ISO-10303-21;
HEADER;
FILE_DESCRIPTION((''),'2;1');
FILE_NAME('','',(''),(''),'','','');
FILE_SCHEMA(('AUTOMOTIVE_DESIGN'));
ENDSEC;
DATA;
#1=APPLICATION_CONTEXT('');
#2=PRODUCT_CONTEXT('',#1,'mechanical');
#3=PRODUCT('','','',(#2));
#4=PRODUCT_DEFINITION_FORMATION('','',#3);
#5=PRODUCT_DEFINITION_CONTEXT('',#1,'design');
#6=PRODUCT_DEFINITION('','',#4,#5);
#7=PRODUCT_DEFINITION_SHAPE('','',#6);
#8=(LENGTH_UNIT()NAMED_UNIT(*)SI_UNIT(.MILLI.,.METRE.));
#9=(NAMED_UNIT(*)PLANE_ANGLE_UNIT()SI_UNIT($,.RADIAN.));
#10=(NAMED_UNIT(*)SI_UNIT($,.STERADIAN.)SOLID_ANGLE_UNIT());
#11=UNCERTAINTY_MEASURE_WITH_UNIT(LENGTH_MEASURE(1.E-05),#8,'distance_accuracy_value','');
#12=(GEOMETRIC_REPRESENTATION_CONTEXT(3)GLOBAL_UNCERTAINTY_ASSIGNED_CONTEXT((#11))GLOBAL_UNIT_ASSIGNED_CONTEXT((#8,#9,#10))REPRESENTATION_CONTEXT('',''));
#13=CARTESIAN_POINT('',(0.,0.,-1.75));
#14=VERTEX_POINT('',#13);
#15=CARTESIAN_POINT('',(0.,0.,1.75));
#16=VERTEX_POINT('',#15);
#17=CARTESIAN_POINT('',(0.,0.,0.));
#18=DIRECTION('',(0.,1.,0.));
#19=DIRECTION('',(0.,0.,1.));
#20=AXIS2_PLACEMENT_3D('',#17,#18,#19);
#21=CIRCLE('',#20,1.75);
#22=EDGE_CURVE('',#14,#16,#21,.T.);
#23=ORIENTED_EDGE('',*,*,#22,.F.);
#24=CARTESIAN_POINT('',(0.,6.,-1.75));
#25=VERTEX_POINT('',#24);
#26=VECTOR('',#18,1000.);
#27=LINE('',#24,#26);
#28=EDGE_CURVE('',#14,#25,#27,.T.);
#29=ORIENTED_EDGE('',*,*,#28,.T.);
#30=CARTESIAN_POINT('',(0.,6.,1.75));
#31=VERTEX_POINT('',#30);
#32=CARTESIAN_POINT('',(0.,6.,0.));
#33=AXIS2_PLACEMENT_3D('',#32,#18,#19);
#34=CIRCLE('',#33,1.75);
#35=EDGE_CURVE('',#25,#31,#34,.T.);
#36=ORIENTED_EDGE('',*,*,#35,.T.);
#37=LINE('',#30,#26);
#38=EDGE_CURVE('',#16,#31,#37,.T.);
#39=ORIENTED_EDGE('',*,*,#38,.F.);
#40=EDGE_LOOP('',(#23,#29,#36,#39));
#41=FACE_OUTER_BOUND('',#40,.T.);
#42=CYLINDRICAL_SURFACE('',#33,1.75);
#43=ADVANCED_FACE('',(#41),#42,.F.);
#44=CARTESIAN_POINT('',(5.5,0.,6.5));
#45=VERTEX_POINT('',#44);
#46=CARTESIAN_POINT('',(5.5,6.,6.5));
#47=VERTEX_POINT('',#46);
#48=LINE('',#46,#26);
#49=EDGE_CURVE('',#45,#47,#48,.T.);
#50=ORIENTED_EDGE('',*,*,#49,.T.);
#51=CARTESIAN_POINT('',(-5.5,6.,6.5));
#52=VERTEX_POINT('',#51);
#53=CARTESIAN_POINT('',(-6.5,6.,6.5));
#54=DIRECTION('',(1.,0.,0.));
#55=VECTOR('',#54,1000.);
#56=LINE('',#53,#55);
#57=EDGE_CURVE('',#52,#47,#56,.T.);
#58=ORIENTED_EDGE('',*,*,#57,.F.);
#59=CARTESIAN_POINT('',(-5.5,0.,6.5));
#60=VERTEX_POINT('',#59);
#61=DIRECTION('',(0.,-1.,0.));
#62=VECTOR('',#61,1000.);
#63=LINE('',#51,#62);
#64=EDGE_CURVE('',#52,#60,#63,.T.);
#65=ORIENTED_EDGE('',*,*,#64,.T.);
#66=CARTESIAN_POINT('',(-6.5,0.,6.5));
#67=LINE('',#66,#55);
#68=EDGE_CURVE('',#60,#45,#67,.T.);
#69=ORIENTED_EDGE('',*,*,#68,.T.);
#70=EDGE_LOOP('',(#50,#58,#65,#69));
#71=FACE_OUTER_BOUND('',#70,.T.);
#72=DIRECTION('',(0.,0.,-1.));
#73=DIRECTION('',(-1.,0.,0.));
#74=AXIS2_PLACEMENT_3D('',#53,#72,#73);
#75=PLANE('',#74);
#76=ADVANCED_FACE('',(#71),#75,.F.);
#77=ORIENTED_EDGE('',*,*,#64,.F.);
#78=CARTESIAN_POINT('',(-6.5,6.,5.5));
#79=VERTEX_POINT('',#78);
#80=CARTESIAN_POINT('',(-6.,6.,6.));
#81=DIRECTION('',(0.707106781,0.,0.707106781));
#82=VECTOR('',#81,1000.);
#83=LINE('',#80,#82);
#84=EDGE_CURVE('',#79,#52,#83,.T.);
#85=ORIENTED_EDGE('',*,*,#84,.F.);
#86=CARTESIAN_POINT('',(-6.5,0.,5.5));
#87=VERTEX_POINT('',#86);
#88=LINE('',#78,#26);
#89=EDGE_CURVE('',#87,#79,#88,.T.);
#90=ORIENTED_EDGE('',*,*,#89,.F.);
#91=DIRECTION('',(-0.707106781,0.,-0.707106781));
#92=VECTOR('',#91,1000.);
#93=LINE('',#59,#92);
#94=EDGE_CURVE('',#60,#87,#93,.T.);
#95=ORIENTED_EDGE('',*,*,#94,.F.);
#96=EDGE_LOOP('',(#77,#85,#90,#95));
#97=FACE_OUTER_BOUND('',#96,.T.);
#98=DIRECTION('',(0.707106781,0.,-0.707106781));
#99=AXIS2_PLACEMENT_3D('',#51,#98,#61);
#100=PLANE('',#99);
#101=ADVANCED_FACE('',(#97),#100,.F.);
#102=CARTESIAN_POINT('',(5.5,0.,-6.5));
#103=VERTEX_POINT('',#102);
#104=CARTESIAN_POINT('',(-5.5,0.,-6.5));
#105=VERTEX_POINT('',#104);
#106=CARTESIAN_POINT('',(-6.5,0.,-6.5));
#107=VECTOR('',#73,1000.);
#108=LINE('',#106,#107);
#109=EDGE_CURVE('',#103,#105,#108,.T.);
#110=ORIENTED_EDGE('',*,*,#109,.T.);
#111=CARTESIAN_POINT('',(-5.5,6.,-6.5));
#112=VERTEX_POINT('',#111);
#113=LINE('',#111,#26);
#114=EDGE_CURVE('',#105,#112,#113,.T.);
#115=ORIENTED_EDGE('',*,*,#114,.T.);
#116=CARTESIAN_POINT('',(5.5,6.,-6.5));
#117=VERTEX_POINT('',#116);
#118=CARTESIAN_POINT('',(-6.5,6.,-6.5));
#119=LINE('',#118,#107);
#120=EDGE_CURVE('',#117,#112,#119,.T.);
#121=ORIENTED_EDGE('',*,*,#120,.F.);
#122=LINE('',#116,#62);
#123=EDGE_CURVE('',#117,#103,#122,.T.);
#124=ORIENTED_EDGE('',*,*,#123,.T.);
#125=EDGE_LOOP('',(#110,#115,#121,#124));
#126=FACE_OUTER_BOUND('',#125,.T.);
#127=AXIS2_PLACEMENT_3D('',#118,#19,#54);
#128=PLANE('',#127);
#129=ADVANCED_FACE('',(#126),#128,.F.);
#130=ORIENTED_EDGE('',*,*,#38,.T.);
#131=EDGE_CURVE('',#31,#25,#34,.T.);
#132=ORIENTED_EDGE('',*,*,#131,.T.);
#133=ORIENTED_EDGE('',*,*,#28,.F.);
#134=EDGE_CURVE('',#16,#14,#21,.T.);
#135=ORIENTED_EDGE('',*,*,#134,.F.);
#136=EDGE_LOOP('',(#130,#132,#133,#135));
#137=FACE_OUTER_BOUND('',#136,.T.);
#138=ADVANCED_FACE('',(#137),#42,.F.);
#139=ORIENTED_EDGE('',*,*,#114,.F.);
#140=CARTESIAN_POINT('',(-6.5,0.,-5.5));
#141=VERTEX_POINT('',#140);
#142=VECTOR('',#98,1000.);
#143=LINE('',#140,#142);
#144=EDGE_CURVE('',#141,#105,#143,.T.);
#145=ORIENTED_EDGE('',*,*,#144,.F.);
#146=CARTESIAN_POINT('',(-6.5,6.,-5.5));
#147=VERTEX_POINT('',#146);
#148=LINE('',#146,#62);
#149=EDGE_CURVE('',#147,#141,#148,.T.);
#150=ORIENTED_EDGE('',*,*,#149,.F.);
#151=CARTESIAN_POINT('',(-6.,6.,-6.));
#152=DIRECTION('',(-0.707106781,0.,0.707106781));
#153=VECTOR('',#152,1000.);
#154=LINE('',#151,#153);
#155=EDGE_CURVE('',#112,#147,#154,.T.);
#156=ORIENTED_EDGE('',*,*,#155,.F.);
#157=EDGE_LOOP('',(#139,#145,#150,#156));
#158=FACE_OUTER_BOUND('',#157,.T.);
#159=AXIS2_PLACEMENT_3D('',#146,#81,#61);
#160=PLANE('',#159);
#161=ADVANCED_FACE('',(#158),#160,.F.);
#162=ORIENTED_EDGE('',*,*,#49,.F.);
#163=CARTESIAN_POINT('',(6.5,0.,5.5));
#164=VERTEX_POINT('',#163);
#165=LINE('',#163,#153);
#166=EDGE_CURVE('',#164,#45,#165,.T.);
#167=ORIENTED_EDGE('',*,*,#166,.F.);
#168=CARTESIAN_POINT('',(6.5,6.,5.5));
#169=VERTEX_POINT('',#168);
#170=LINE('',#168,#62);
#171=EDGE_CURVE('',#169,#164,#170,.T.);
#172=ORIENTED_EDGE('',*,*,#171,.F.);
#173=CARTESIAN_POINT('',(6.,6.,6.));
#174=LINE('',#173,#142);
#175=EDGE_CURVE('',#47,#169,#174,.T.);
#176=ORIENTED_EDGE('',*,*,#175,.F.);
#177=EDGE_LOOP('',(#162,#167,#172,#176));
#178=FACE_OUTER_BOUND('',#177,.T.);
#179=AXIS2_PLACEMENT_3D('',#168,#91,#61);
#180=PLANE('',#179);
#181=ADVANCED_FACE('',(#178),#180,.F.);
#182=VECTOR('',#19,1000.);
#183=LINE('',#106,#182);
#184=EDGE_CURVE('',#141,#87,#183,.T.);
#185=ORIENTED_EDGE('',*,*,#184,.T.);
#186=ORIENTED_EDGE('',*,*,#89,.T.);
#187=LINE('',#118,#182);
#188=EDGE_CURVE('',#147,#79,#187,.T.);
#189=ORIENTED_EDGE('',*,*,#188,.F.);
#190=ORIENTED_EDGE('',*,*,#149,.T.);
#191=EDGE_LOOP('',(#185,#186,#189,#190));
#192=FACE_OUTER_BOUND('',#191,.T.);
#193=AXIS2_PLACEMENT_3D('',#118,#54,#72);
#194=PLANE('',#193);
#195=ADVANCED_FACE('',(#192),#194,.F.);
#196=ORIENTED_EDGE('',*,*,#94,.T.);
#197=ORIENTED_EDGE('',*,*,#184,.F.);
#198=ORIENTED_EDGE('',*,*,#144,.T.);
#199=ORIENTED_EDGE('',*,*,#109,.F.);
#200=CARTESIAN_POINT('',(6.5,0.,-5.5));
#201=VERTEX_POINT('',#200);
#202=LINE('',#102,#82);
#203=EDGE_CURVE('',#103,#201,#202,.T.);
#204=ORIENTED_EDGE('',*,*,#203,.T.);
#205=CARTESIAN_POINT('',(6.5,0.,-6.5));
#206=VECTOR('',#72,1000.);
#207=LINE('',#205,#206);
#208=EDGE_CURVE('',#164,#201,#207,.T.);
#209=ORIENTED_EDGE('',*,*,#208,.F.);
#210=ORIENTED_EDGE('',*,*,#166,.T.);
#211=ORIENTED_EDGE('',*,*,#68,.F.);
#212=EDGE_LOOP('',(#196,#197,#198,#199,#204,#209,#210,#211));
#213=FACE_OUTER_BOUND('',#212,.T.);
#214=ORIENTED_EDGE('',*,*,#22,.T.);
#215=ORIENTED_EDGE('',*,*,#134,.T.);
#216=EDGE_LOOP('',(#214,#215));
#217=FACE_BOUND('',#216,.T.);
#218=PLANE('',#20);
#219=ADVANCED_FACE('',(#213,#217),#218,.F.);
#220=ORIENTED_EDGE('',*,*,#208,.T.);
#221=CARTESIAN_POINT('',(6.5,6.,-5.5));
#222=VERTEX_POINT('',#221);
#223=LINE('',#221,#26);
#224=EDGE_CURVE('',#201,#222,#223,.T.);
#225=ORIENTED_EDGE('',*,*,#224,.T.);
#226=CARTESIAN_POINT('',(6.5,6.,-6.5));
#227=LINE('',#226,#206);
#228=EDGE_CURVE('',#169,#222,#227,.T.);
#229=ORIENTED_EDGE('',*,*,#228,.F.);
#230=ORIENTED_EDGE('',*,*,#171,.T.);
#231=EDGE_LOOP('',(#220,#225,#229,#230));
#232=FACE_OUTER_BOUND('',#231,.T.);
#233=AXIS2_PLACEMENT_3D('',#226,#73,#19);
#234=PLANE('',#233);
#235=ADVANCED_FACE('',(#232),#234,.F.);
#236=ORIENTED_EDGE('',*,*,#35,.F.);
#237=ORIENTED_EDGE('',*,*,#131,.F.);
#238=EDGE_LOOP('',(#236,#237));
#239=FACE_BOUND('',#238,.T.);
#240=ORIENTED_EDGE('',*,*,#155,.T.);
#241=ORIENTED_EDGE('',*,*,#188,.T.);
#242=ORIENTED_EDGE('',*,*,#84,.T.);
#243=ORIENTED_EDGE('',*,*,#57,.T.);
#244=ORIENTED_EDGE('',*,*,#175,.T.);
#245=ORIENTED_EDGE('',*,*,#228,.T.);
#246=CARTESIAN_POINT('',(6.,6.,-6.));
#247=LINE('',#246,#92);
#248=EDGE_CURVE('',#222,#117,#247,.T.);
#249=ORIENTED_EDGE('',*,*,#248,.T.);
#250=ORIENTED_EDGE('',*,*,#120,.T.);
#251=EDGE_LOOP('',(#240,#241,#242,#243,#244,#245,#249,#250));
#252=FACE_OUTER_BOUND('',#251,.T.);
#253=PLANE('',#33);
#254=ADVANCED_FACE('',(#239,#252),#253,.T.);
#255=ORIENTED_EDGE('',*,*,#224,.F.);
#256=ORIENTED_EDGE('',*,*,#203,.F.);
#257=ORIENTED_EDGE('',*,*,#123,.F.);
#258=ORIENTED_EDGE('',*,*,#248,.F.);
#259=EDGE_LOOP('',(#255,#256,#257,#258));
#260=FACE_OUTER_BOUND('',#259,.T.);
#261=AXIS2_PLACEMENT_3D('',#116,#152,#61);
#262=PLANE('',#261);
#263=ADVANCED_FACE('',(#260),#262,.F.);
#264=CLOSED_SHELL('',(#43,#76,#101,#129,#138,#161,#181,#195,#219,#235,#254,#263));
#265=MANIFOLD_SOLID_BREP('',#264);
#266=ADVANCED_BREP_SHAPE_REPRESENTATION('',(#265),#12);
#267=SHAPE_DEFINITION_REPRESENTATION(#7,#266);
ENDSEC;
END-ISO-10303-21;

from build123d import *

# Parameters (mm, degrees)
SKETCH_1_W              = 13
SKETCH_1_H              = 13
EXTRUDE_1_DEPTH         = 6
HOLE_WIZARD_3_5_3_5_1_D = 3.5
CHAMFER_1_SIZE          = 1


with BuildPart() as part:
    # 草图1 → 凸台-拉伸1 (new body)
    with BuildSketch(Plane(origin=(0, 0, 0), x_dir=(1, 0, 0), z_dir=(0, 1, 0))):
        Rectangle(SKETCH_1_W, SKETCH_1_H)
    extrude(amount=EXTRUDE_1_DEPTH)

    # Ø3.5 (3.5) 直径孔1 (through all)
    with Locations(Plane(origin=(0, 6, 0), x_dir=(1, 0, 0), z_dir=(0, 1, 0))):
        with Locations((0, 0)):
            Hole(HOLE_WIZARD_3_5_3_5_1_D / 2)

    # 倒角1
    chamfer_1_edges = [part.edges().sort_by_distance(p)[0] for p in [
        (6.5, 3, 6.5),
        (-6.5, 3, 6.5),
        (-6.5, 3, -6.5),
        (6.5, 3, -6.5),
    ]]
    chamfer(chamfer_1_edges, length=CHAMFER_1_SIZE)


solid = part.part
